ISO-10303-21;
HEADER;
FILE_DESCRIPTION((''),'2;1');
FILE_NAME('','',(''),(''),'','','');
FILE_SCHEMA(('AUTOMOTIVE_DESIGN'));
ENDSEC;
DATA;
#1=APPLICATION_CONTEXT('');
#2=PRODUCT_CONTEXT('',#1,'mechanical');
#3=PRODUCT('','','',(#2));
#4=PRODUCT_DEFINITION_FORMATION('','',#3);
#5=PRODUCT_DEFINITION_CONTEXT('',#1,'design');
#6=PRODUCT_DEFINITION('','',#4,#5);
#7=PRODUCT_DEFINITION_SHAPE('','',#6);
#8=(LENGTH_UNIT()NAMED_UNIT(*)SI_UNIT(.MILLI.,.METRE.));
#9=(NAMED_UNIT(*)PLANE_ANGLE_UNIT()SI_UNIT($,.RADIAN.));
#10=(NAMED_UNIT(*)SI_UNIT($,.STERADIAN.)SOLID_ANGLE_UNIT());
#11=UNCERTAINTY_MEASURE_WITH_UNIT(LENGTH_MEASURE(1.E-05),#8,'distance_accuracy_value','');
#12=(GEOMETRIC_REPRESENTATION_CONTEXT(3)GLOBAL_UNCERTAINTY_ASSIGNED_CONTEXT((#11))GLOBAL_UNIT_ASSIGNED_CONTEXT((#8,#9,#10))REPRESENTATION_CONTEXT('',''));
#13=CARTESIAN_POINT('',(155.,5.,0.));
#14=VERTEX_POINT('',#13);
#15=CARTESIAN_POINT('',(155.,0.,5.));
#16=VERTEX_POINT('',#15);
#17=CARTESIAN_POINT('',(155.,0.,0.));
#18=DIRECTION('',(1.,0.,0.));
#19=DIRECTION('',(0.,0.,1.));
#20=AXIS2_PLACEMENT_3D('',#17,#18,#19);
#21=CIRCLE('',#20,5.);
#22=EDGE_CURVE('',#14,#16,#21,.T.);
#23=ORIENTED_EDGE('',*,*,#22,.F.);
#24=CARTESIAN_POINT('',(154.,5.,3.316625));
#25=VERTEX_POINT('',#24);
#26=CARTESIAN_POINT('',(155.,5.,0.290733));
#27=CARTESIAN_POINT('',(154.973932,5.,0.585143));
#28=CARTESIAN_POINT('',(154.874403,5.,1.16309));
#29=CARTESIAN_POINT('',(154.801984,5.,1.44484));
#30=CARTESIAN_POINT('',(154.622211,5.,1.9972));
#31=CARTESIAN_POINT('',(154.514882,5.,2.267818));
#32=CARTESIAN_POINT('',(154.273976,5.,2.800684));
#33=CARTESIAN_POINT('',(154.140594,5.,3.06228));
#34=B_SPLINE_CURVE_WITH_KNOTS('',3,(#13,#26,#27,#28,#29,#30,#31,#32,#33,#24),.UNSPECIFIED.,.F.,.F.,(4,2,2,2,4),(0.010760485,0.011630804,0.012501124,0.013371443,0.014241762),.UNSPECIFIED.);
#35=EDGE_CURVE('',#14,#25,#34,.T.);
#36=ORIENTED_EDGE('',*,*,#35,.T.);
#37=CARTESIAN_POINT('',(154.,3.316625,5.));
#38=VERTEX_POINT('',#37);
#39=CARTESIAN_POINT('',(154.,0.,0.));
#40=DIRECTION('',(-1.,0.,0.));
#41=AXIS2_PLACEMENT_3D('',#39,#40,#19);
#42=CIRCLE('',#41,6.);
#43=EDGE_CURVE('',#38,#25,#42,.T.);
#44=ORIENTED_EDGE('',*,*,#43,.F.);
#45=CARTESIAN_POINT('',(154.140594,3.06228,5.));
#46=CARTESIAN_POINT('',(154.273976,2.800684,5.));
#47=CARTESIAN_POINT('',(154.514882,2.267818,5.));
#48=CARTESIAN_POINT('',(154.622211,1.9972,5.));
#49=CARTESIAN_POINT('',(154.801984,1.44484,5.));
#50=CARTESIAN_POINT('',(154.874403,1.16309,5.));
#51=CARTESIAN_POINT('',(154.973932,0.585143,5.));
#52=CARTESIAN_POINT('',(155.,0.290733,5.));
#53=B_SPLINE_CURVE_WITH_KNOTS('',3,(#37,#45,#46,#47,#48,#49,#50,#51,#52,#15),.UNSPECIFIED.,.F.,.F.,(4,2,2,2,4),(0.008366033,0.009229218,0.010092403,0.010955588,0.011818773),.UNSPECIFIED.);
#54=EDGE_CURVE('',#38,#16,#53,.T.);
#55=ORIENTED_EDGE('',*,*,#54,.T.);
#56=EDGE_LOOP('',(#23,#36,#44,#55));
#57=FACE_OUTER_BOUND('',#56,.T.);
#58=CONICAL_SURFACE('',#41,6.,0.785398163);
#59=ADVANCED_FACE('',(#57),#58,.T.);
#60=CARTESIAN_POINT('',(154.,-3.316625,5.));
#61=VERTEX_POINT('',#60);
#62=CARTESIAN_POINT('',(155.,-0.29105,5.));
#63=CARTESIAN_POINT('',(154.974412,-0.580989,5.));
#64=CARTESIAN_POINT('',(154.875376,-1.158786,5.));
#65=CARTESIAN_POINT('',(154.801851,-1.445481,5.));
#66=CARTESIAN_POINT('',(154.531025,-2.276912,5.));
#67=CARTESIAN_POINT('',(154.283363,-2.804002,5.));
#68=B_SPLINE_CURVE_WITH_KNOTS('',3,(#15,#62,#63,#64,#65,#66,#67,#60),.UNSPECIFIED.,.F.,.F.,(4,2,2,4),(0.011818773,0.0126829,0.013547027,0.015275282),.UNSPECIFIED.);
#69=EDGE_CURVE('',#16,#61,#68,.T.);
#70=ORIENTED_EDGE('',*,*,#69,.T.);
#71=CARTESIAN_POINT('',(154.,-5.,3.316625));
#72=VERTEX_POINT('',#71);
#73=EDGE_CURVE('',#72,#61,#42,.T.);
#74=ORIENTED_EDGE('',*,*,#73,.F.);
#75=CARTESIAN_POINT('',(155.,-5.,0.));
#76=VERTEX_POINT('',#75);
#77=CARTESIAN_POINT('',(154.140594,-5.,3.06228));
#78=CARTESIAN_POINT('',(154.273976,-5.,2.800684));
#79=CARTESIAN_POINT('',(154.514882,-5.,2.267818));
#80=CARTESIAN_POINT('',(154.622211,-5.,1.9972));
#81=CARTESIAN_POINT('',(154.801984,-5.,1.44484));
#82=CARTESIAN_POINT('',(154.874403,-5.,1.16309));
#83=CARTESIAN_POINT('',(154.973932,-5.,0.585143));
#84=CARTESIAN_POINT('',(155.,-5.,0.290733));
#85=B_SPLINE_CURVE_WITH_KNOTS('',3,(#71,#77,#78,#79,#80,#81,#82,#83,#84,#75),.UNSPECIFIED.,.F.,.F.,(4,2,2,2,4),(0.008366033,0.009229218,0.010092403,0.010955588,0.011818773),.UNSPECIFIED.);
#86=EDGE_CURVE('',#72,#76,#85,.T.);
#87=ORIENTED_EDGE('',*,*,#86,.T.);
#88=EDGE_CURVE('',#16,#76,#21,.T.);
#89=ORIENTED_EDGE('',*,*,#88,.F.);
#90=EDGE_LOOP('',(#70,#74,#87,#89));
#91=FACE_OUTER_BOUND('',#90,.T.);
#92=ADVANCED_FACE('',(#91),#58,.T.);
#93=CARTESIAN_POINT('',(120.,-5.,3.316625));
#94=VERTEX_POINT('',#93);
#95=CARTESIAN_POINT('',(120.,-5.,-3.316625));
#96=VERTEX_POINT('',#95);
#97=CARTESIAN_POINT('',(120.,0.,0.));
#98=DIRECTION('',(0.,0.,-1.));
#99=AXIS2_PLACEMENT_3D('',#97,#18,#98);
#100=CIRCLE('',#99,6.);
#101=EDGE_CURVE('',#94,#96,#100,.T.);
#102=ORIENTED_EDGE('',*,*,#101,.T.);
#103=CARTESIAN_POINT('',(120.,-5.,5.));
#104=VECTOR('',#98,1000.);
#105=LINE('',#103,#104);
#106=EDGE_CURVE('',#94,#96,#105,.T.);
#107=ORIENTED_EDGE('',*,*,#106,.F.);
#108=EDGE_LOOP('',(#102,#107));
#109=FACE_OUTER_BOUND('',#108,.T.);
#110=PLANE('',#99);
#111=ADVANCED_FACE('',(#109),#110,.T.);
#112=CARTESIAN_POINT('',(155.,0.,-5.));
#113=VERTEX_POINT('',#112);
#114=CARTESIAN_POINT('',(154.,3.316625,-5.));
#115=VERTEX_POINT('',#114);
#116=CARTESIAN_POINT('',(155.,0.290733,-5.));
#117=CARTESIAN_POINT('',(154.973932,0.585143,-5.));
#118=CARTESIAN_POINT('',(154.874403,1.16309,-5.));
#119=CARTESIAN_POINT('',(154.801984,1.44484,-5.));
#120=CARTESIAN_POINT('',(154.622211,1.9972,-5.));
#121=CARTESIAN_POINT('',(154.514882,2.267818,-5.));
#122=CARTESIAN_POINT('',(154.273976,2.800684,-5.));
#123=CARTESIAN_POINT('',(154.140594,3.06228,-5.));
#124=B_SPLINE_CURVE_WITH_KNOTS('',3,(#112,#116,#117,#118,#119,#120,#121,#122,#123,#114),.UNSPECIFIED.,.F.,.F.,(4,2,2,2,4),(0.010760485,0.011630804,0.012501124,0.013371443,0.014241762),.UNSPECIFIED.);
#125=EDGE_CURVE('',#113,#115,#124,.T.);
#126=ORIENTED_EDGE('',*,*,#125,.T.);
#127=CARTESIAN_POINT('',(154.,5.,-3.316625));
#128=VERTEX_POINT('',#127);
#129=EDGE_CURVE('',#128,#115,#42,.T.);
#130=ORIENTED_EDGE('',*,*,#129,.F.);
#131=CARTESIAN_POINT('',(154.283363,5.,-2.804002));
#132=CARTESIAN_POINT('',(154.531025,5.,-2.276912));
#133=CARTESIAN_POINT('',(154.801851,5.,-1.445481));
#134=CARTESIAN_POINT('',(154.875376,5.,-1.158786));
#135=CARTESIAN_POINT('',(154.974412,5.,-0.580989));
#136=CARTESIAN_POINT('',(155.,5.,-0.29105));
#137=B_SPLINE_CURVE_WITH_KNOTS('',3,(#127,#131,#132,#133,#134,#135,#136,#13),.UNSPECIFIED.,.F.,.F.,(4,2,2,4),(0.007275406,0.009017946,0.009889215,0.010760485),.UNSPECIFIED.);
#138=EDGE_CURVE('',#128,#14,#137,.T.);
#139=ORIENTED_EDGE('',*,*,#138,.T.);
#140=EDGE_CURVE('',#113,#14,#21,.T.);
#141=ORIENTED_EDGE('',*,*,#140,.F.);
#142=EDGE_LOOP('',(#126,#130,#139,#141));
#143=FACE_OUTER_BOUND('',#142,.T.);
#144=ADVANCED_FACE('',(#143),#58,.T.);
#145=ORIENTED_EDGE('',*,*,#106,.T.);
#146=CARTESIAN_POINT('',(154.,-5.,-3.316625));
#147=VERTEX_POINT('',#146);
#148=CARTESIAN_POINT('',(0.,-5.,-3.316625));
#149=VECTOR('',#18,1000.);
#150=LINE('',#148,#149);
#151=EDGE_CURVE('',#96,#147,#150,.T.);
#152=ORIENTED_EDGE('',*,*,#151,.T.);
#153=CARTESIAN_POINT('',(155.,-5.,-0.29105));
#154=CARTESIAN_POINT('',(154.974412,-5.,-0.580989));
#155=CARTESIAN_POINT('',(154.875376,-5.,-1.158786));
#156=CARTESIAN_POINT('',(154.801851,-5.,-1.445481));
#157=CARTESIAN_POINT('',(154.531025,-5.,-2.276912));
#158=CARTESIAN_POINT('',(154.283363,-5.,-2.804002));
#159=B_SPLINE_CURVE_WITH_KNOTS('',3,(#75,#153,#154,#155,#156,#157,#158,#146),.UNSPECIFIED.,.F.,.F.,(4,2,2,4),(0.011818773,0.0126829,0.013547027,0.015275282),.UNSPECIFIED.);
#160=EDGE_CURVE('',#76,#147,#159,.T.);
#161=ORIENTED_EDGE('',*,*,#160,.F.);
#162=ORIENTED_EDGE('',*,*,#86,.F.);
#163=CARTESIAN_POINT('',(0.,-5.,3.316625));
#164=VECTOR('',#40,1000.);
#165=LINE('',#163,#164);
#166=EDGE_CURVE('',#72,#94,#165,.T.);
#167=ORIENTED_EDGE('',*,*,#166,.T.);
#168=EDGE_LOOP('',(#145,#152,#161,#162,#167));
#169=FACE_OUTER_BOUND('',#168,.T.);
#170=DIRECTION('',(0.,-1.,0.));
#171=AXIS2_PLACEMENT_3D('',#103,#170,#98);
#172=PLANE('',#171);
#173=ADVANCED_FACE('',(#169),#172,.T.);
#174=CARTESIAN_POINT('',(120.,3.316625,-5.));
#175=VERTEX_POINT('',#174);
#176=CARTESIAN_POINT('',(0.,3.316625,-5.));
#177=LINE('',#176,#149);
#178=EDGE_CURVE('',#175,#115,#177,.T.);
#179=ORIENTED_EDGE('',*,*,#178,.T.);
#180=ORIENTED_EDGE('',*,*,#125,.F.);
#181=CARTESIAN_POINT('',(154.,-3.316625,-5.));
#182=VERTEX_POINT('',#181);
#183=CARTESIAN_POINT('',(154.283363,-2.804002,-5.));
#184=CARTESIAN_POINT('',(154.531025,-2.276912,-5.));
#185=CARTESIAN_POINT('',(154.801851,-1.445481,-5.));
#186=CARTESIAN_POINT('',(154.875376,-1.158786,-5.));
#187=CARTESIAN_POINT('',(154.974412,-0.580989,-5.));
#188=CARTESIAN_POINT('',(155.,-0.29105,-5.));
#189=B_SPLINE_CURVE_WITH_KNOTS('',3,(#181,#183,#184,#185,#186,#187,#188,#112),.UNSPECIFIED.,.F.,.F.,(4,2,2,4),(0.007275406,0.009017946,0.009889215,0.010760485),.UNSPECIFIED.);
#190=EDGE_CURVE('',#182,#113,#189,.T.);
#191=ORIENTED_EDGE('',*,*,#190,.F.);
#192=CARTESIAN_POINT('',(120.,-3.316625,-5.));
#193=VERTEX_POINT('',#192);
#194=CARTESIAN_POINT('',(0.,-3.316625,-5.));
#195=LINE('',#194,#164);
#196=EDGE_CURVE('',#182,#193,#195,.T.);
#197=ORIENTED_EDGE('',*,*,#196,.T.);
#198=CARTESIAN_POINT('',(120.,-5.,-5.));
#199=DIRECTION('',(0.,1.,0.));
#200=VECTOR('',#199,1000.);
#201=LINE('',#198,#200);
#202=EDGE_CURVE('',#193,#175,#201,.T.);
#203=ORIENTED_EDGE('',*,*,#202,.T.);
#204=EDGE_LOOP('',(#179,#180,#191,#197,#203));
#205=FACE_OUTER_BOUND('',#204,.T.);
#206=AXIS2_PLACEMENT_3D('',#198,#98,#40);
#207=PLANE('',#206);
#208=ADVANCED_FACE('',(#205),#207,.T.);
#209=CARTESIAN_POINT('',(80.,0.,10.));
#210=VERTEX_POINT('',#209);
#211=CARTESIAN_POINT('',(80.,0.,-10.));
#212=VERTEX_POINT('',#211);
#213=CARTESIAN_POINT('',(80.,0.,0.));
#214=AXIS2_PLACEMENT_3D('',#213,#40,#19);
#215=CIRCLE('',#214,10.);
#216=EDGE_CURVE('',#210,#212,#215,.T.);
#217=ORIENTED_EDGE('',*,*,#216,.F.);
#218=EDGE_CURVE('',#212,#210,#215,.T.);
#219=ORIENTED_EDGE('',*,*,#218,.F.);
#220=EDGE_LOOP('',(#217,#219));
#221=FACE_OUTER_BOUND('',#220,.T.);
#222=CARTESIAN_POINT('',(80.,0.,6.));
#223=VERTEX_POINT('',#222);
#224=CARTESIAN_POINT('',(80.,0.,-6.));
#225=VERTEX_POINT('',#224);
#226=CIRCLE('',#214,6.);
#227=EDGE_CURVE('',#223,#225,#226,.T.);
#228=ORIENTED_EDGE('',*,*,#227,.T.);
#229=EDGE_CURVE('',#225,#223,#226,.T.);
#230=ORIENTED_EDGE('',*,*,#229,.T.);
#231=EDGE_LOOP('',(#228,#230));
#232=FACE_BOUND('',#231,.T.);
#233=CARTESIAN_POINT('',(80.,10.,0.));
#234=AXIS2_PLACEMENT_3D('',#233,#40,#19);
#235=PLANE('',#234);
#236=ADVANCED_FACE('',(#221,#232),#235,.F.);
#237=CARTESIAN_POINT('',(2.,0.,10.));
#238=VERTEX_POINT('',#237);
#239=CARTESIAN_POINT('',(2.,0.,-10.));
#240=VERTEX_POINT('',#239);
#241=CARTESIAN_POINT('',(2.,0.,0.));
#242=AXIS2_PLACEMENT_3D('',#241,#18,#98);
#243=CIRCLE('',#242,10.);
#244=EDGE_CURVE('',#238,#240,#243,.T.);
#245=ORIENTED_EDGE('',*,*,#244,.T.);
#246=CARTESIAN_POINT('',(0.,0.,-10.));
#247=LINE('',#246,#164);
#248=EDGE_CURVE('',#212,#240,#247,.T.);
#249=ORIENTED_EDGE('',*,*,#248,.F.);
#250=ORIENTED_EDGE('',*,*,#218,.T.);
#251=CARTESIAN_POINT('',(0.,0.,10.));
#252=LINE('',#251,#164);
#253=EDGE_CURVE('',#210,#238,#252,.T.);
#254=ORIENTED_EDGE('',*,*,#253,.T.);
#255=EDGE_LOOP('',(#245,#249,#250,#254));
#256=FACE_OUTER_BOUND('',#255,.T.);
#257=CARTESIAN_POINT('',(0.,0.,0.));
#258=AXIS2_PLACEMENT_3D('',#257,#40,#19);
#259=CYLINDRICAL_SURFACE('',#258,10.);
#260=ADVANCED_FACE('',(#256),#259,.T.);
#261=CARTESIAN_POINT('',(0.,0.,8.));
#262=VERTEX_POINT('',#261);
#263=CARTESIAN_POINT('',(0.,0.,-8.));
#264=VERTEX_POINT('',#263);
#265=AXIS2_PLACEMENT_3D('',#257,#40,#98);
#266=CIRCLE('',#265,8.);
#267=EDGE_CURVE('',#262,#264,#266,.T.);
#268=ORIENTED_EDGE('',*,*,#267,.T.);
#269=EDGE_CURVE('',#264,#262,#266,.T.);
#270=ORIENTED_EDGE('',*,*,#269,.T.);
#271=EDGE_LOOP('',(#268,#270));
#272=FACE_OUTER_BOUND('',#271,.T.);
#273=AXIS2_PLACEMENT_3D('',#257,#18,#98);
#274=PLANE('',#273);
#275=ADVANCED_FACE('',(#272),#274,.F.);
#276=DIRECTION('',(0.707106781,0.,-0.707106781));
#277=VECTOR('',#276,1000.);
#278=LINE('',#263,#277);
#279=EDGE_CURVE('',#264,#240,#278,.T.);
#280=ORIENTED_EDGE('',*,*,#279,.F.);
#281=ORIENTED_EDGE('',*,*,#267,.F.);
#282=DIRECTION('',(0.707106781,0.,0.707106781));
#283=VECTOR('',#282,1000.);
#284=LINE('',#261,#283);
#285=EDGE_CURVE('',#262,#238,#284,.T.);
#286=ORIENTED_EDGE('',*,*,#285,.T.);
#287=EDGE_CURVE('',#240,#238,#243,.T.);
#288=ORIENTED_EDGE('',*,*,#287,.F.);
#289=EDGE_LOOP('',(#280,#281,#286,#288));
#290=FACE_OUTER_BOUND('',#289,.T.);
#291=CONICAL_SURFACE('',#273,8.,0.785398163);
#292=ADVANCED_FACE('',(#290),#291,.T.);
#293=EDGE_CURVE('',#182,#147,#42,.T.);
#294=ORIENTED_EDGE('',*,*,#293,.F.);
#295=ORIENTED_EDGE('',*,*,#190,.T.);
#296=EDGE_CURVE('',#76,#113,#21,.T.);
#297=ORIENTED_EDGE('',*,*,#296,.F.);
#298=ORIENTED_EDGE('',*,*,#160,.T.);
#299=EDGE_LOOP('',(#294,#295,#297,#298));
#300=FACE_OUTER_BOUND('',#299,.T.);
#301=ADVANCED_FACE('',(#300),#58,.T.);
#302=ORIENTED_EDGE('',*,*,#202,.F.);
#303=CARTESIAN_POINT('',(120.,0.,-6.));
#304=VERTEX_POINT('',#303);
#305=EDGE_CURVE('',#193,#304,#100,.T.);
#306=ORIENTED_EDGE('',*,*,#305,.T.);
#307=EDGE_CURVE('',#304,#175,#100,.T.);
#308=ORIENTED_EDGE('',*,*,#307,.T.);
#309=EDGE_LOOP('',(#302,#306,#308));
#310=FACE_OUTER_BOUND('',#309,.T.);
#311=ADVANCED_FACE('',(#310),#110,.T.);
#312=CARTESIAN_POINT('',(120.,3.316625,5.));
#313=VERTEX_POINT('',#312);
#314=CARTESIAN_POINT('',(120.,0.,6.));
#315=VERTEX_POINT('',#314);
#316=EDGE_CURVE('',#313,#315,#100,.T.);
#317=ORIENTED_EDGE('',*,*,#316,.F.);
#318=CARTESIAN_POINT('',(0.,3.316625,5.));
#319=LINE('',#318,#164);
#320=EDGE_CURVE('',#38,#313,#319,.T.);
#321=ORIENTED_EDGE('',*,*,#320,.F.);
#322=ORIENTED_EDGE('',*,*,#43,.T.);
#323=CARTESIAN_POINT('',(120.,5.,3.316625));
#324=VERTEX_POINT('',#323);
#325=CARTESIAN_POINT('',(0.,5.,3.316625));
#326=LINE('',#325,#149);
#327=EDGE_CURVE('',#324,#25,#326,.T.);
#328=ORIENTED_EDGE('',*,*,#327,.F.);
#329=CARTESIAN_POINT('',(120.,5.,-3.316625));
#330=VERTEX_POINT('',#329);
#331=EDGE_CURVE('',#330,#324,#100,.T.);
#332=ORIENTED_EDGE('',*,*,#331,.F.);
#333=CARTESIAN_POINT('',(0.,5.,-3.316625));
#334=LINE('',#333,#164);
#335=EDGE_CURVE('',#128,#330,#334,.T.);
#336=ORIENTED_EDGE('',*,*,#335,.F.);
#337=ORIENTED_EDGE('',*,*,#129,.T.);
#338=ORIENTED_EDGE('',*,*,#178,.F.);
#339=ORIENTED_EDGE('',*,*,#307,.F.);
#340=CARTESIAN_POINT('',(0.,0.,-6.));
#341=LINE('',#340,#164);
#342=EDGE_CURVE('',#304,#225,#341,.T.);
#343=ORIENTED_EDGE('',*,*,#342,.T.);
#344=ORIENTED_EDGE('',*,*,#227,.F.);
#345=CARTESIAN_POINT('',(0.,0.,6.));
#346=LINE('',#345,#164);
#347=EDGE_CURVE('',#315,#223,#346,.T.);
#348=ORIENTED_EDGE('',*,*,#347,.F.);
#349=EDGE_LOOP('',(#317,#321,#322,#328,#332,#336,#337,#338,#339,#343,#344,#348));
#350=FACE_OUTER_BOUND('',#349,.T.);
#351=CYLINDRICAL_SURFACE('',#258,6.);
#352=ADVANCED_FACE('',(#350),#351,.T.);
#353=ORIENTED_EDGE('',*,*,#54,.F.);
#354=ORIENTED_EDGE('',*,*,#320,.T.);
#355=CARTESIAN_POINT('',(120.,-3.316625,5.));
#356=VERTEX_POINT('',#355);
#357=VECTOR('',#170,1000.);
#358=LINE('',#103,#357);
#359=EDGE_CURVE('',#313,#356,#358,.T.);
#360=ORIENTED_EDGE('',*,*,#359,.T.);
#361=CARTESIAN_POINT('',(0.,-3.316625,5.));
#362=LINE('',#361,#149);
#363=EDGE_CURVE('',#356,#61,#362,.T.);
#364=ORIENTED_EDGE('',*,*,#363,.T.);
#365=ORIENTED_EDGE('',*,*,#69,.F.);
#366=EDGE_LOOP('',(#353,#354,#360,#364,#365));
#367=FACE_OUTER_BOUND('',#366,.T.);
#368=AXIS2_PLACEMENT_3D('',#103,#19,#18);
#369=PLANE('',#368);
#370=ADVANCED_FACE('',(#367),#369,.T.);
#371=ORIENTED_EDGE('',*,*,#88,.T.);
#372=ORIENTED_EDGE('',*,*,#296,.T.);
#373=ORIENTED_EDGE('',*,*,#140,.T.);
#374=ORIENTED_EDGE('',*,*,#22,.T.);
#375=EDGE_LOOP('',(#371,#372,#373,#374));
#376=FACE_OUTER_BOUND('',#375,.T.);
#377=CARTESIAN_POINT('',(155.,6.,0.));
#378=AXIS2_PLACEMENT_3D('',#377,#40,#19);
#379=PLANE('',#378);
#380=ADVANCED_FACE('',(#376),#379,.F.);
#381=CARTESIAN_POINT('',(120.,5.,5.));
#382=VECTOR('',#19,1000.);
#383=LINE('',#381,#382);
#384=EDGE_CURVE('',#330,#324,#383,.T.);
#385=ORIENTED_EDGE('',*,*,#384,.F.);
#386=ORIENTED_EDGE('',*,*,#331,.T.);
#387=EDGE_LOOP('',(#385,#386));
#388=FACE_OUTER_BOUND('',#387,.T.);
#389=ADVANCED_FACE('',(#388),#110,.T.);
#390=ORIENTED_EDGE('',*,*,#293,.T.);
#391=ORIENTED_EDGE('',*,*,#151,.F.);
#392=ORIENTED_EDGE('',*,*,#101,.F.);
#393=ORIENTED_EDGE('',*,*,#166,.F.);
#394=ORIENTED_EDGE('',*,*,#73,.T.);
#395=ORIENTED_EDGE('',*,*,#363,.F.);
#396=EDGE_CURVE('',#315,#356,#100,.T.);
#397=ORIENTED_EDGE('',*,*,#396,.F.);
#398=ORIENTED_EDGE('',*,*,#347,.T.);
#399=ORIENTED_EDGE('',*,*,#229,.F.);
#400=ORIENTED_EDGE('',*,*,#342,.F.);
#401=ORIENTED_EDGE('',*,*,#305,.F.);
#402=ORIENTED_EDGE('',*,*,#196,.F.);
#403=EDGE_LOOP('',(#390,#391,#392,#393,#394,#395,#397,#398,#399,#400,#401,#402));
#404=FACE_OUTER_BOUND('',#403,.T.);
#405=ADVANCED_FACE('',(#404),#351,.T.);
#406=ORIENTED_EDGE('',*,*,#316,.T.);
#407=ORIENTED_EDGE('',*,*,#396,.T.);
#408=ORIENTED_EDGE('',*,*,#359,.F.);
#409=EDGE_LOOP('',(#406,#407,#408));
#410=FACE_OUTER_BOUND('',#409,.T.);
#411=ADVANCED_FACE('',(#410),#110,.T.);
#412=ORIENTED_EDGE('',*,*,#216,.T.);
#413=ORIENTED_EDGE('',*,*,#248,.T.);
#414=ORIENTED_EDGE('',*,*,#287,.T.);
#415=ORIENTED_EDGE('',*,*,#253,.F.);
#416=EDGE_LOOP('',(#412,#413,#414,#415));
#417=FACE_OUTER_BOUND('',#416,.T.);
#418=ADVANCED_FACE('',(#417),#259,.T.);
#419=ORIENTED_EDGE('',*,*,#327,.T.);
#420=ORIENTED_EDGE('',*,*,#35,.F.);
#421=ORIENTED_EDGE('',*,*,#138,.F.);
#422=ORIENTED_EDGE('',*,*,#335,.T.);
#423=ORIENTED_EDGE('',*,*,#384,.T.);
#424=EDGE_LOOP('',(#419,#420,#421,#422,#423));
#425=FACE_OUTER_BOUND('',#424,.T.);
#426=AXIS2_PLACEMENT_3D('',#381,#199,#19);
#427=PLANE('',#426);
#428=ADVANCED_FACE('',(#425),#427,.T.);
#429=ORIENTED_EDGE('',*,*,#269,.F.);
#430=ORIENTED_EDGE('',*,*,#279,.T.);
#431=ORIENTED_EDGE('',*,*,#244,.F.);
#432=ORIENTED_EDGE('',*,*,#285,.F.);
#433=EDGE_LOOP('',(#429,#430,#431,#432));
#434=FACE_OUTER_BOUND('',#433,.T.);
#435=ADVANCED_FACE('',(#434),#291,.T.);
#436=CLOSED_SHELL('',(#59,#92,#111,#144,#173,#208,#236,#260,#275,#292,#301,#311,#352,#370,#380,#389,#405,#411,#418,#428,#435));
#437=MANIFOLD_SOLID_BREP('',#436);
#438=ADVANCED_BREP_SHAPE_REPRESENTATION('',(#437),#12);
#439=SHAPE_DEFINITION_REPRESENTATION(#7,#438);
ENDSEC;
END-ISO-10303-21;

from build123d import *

# Parameters (mm, degrees)
CHAMFER1_SIZE       = 1
CHAMFER2_SIZE       = 2
SKETCH2_OUTSIDE_W   = 53.512
SKETCH2_OUTSIDE_H   = 53.512
SKETCH2_OUTSIDE_W_2 = 10
SKETCH2_OUTSIDE_H_2 = 10
CUT_EXTRUDE1_DEPTH  = 35


with BuildPart() as part:
    # Sketch1 → Revolve1 (revolve)
    with BuildSketch(Plane.XY, mode=Mode.PRIVATE) as revolve1_sk:
        Polygon((0, 0), (0, 10), (80, 10), (80, 6), (155, 6), (155, 0), align=None)
    revolve(revolve1_sk.sketch.rotate(Axis((0, 0, 0), (1, 0, 0)), 90), axis=Axis((0, 0, 0), (1, 0, 0)))

    # Chamfer1
    chamfer1_edges = [part.edges().sort_by_distance(p)[0] for p in [
        (155, 0, -6),
    ]]
    chamfer(chamfer1_edges, length=CHAMFER1_SIZE)

    # Chamfer2
    chamfer2_edges = [part.edges().sort_by_distance(p)[0] for p in [
        (0, 0, -10),
    ]]
    chamfer(chamfer2_edges, length=CHAMFER2_SIZE)

    # Sketch2 outside → Cut-Extrude1 (cut)
    with BuildSketch(Plane(origin=(155, 0, 0), x_dir=(0, 0, -1), z_dir=(1, 0, 0))):
        Rectangle(SKETCH2_OUTSIDE_W, SKETCH2_OUTSIDE_H)
        Rectangle(SKETCH2_OUTSIDE_W_2, SKETCH2_OUTSIDE_H_2, mode=Mode.SUBTRACT)
    extrude(amount=-CUT_EXTRUDE1_DEPTH, mode=Mode.SUBTRACT)


solid = part.part
